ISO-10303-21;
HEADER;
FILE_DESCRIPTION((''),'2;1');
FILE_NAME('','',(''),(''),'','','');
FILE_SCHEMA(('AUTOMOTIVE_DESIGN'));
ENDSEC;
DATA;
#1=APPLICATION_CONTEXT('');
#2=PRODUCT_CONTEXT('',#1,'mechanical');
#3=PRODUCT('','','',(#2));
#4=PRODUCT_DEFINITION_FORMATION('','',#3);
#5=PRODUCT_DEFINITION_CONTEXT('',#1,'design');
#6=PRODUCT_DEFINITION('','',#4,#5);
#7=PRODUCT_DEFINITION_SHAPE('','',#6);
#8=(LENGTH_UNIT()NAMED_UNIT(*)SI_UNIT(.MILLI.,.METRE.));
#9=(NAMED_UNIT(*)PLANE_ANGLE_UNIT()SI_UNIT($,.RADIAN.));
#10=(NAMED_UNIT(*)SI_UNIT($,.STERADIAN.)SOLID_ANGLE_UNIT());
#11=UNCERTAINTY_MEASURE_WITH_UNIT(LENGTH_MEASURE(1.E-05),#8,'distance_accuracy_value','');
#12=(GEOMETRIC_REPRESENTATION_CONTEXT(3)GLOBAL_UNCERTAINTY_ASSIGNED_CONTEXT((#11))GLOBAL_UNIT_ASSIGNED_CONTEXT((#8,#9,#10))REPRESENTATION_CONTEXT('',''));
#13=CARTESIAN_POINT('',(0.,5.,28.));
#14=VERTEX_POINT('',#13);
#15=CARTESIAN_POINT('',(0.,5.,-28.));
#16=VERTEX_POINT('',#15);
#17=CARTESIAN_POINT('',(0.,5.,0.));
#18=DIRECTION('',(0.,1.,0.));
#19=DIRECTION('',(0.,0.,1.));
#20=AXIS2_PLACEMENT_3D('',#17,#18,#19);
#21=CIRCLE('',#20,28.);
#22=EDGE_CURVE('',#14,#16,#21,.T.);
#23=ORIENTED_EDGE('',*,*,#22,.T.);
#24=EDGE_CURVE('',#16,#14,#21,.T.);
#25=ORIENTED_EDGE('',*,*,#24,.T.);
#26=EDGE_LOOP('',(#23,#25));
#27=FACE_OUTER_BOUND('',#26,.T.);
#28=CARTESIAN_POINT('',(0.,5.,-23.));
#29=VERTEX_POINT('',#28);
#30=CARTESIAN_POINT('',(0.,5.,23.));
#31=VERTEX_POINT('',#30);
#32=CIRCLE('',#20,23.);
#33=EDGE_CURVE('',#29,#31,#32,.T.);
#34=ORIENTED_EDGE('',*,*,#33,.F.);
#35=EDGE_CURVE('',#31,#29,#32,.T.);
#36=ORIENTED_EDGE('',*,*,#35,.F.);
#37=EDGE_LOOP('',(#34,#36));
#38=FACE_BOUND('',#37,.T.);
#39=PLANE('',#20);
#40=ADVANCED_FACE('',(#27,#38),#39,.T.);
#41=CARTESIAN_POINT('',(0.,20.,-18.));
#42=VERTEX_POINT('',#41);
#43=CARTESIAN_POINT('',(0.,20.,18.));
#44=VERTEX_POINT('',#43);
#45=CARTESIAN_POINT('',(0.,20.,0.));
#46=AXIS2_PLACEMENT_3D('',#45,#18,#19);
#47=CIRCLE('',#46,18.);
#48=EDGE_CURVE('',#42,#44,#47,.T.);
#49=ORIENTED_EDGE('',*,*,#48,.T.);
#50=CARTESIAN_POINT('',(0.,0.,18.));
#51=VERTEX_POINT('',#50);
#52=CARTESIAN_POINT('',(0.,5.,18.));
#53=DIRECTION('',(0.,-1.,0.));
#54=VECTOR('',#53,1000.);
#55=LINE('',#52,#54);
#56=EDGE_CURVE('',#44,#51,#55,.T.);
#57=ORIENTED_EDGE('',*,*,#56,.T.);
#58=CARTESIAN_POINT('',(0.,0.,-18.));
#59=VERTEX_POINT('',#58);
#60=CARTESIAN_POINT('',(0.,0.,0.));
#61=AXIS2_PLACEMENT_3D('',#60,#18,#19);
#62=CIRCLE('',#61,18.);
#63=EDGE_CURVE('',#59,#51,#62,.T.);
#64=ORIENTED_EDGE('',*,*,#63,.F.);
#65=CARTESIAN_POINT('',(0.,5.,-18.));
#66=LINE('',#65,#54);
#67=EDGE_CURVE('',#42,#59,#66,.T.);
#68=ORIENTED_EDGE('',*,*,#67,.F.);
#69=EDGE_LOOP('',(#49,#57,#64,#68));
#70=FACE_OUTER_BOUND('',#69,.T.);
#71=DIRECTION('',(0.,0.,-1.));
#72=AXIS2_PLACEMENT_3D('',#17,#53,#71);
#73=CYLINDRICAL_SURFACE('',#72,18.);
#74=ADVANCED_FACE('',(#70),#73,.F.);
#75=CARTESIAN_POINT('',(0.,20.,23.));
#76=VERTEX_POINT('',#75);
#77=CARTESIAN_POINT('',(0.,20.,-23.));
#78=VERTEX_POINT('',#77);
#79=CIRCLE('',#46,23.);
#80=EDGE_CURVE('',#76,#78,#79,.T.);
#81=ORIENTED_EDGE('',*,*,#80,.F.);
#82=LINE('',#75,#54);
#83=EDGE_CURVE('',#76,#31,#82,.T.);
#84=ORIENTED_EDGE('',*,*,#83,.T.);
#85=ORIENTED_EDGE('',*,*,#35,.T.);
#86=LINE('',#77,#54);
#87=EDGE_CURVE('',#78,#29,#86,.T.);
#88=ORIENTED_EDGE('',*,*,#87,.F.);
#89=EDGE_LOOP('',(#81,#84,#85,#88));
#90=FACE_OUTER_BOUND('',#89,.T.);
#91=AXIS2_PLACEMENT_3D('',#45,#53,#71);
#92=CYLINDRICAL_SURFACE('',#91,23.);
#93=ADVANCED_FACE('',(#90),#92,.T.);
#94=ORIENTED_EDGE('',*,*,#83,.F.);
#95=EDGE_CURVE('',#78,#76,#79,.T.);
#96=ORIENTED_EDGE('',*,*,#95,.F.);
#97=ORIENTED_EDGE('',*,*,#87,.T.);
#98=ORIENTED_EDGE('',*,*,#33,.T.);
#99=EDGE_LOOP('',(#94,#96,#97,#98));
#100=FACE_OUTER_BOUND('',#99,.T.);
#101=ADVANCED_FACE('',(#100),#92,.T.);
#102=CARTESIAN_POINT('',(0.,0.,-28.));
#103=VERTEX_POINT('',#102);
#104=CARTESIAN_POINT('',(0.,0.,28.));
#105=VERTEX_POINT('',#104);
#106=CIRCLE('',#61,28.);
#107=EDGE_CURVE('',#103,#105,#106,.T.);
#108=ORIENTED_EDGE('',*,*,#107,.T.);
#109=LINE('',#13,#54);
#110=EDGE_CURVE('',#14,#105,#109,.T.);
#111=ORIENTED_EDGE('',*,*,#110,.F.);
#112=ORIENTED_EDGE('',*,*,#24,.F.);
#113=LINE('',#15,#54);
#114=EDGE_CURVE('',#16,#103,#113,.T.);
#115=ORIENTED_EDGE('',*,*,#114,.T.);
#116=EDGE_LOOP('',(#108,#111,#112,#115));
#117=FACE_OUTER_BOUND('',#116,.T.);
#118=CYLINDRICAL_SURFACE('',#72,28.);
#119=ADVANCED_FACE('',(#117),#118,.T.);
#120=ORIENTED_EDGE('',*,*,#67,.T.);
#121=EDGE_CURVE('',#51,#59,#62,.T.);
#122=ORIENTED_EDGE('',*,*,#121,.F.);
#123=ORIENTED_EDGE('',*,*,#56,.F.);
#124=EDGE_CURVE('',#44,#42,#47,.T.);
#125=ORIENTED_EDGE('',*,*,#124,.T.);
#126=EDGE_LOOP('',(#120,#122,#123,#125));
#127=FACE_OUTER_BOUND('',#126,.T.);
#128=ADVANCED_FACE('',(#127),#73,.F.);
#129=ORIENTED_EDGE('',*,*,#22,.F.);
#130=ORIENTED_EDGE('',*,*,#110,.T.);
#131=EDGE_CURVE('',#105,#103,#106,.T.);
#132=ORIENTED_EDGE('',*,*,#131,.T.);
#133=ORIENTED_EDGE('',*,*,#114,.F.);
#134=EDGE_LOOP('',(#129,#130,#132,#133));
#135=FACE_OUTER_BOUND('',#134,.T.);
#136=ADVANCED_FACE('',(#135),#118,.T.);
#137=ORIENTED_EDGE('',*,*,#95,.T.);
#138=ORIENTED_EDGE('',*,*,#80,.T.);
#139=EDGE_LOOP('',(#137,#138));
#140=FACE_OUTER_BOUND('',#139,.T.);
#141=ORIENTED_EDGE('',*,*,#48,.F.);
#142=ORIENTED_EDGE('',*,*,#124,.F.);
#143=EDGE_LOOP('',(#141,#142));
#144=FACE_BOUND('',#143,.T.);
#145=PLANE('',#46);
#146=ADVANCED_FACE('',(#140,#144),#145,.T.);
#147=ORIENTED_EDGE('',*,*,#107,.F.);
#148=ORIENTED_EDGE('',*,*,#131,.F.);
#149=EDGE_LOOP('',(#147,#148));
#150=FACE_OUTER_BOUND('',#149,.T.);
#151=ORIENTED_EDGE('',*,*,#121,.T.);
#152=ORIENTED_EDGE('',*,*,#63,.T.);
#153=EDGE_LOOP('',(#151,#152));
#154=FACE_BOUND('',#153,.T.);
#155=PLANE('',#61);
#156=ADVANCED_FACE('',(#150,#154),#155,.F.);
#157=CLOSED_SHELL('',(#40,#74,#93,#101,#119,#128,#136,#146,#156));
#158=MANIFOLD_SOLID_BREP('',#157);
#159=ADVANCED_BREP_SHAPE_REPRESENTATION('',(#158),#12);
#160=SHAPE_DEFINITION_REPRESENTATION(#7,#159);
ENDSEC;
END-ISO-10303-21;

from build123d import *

# Parameters (mm, degrees)
SKETCH_1_R      = 28
SKETCH_1_R_2    = 18
EXTRUDE_1_DEPTH = 5
SKETCH_2_R      = 23
SKETCH_2_R_2    = 18
EXTRUDE_2_DEPTH = 15


with BuildPart() as part:
    # 草图1 → 凸台-拉伸1 (new body)
    with BuildSketch(Plane(origin=(0, 0, 0), x_dir=(1, 0, 0), z_dir=(0, 1, 0))):
        with Locations(Location((0, 0, 0), (0, 0, 270))):
            Circle(SKETCH_1_R)
        with Locations(Location((0, 0, 0), (0, 0, 270))):
            Circle(SKETCH_1_R_2, mode=Mode.SUBTRACT)
    extrude(amount=EXTRUDE_1_DEPTH)

    # 草图2 → 凸台-拉伸2 (add)
    with BuildSketch(Plane(origin=(0, 5, 0), x_dir=(1, 0, 0), z_dir=(0, 1, 0))):
        with Locations(Location((0, 0, 0), (0, 0, 270))):
            Circle(SKETCH_2_R)
        with Locations(Location((0, 0, 0), (0, 0, 270))):
            Circle(SKETCH_2_R_2, mode=Mode.SUBTRACT)
    extrude(amount=EXTRUDE_2_DEPTH)


solid = part.part
